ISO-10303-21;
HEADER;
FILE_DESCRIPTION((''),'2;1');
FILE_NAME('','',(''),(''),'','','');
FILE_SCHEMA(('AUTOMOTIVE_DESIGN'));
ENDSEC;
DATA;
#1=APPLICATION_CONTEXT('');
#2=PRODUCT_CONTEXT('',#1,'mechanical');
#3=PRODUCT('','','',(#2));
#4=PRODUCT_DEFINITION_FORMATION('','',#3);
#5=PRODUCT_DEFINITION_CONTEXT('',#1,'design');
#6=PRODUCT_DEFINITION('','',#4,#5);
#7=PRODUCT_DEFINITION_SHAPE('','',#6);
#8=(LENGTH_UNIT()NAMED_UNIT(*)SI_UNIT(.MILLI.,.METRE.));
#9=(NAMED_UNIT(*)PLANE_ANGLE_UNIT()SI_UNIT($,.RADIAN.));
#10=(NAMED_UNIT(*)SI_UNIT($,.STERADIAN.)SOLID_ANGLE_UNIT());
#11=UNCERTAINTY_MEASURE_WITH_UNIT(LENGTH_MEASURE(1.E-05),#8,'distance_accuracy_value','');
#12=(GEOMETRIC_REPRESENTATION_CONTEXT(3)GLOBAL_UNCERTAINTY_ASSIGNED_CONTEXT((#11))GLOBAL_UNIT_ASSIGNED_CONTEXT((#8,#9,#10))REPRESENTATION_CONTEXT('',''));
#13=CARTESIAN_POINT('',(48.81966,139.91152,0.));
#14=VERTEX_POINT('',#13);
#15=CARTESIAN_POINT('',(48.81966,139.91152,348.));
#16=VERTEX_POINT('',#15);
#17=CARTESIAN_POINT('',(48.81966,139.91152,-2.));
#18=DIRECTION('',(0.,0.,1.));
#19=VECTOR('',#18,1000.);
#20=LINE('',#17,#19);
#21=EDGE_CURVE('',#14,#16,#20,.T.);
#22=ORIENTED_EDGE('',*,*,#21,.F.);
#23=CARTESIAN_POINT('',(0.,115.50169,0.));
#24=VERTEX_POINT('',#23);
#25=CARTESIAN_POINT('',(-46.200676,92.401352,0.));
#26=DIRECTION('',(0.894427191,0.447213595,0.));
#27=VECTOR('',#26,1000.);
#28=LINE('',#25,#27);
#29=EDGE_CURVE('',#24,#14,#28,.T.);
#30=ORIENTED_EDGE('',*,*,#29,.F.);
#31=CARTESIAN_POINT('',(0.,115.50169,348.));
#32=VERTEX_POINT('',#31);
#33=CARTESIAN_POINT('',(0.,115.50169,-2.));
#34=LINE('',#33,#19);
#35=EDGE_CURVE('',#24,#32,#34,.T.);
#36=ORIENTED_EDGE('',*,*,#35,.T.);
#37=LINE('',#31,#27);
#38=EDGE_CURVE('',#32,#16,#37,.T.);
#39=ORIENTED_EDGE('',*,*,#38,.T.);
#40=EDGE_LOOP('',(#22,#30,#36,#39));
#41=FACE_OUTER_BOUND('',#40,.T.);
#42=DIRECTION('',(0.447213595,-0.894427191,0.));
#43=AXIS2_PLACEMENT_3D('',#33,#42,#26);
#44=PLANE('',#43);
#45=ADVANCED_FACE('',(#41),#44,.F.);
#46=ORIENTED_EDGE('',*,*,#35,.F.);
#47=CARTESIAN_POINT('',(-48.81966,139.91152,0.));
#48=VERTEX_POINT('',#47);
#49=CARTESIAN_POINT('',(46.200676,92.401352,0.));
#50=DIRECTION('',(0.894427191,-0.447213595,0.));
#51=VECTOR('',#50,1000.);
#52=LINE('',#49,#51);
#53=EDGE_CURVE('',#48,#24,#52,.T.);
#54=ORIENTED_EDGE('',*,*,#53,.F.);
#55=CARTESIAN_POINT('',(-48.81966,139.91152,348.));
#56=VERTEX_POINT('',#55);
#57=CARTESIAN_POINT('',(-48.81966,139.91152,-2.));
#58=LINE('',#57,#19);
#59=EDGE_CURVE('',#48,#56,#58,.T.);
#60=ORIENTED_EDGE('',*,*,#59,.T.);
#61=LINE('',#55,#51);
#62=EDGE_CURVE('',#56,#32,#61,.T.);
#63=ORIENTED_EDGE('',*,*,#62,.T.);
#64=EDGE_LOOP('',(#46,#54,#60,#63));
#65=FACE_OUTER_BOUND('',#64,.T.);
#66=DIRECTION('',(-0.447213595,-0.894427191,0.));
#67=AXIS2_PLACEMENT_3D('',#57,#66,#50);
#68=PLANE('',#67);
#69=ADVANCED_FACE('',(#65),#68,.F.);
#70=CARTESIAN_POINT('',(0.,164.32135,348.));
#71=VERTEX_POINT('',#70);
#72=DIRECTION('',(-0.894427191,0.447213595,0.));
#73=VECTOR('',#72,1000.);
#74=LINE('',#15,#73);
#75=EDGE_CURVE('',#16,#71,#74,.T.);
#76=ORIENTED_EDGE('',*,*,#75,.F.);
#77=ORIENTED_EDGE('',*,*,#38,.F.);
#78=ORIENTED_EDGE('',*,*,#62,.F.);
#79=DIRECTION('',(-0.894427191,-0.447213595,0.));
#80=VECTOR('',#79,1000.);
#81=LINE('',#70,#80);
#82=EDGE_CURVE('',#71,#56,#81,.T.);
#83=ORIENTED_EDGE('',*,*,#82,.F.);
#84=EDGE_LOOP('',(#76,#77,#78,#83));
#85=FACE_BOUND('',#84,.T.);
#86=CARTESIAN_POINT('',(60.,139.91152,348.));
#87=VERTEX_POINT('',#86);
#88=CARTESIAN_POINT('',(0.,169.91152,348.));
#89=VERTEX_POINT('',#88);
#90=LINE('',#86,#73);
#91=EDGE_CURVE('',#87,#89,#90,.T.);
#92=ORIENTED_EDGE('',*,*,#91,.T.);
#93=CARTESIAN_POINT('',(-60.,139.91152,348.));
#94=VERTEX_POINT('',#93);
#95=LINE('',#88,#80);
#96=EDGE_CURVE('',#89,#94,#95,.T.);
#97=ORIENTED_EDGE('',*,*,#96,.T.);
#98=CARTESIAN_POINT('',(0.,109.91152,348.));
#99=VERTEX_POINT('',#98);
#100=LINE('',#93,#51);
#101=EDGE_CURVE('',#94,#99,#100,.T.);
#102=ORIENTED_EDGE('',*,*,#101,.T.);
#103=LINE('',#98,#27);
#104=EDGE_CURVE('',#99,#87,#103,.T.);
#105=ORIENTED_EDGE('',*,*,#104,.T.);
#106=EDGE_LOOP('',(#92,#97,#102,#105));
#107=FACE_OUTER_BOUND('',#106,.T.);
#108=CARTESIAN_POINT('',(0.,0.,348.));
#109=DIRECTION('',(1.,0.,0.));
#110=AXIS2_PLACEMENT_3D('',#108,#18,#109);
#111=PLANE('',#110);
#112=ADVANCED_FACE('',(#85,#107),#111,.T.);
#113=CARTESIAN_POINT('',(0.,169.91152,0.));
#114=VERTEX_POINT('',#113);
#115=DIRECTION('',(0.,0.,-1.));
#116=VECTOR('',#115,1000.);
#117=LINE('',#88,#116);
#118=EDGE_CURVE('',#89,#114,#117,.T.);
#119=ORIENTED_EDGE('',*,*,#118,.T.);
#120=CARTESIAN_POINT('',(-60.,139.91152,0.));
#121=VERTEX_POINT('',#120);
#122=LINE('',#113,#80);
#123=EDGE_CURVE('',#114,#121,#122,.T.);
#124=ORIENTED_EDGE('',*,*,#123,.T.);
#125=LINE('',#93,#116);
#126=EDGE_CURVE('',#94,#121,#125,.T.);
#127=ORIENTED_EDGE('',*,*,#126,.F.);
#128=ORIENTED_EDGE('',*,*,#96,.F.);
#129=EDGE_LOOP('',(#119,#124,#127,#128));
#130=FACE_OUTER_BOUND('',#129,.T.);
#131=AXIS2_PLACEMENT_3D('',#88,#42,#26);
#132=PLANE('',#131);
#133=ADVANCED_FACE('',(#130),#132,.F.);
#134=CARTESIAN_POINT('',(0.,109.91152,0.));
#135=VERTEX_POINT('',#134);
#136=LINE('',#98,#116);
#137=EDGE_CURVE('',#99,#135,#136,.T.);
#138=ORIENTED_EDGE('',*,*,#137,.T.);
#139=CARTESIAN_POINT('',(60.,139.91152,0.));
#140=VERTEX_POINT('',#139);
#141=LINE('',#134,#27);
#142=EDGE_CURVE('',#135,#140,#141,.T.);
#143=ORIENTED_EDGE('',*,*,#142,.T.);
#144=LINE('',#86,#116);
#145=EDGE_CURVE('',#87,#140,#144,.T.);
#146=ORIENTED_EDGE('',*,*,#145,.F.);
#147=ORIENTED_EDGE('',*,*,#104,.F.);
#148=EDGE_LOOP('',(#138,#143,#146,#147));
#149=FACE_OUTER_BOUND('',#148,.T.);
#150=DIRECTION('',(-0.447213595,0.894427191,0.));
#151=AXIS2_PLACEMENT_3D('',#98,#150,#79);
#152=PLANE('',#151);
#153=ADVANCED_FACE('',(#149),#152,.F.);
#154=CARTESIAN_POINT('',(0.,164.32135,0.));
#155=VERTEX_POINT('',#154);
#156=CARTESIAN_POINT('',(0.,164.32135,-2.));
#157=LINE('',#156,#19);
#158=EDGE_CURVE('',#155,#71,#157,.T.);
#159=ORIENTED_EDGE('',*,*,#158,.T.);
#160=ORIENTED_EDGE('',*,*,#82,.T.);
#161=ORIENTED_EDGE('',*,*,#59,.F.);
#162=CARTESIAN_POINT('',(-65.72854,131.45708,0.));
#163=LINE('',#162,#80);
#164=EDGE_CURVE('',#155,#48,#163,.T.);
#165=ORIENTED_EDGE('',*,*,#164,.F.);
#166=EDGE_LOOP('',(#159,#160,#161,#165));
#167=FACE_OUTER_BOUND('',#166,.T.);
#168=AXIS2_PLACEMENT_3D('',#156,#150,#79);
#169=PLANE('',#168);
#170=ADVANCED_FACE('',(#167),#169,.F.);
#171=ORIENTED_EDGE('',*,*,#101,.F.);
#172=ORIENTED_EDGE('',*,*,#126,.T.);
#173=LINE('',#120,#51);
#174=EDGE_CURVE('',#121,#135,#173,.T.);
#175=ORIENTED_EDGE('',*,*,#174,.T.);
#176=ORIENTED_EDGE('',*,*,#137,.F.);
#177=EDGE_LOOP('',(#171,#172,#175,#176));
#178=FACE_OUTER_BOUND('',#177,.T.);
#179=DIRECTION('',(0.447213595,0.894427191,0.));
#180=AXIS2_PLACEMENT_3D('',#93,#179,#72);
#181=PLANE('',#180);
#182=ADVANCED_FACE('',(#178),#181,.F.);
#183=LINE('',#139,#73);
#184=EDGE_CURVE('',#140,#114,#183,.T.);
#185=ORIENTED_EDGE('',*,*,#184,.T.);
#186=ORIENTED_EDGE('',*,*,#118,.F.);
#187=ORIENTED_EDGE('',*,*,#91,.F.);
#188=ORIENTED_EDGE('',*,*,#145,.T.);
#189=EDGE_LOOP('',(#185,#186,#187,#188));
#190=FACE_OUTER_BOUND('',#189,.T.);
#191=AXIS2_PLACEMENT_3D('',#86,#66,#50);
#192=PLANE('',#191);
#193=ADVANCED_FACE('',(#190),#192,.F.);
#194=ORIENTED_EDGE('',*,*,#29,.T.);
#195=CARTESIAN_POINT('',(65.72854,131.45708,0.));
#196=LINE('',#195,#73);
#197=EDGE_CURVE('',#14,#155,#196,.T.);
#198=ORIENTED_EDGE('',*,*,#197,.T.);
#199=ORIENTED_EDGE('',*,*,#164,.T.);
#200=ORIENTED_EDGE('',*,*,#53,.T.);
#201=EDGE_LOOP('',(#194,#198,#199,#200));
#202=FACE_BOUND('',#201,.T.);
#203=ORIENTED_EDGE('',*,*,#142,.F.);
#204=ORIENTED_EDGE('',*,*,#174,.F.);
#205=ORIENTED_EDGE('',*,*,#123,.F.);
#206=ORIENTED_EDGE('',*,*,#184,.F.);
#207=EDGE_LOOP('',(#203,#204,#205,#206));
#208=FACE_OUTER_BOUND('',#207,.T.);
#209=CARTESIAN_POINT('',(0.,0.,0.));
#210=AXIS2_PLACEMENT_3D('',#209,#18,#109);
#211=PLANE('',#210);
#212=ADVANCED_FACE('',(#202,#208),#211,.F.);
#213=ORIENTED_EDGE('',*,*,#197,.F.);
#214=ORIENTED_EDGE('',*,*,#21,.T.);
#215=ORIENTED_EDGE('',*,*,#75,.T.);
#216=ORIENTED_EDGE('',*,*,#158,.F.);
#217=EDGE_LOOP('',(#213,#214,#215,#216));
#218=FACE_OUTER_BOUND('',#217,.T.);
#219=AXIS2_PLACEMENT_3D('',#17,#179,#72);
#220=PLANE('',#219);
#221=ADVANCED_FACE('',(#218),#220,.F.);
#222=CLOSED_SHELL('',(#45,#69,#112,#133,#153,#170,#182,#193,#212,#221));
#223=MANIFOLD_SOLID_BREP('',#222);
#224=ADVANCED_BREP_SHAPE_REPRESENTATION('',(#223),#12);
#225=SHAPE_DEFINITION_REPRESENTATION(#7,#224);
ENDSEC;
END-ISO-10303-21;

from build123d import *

# Parameters (mm, degrees)
BOSS_EXTRUDE1_DEPTH = 348
CUT_EXTRUDE1_DEPTH  = 350


with BuildPart() as part:
    # Sketch1 → Boss-Extrude1 (new body)
    with BuildSketch(Plane.XY):
        Polygon((0, 169.911519959), (-60, 139.911519959), (0, 109.911519959), (60, 139.911519959), align=None)
    extrude(amount=BOSS_EXTRUDE1_DEPTH)

    # Sketch2 → Cut-Extrude1 (cut)
    with BuildSketch(Plane.XY.offset(348)):
        Polygon((48.819660113, 139.911519959), (0, 164.321350015), (-48.819660113, 139.911519959), (0, 115.501689902), align=None)
    extrude(amount=-CUT_EXTRUDE1_DEPTH, mode=Mode.SUBTRACT)


solid = part.part
